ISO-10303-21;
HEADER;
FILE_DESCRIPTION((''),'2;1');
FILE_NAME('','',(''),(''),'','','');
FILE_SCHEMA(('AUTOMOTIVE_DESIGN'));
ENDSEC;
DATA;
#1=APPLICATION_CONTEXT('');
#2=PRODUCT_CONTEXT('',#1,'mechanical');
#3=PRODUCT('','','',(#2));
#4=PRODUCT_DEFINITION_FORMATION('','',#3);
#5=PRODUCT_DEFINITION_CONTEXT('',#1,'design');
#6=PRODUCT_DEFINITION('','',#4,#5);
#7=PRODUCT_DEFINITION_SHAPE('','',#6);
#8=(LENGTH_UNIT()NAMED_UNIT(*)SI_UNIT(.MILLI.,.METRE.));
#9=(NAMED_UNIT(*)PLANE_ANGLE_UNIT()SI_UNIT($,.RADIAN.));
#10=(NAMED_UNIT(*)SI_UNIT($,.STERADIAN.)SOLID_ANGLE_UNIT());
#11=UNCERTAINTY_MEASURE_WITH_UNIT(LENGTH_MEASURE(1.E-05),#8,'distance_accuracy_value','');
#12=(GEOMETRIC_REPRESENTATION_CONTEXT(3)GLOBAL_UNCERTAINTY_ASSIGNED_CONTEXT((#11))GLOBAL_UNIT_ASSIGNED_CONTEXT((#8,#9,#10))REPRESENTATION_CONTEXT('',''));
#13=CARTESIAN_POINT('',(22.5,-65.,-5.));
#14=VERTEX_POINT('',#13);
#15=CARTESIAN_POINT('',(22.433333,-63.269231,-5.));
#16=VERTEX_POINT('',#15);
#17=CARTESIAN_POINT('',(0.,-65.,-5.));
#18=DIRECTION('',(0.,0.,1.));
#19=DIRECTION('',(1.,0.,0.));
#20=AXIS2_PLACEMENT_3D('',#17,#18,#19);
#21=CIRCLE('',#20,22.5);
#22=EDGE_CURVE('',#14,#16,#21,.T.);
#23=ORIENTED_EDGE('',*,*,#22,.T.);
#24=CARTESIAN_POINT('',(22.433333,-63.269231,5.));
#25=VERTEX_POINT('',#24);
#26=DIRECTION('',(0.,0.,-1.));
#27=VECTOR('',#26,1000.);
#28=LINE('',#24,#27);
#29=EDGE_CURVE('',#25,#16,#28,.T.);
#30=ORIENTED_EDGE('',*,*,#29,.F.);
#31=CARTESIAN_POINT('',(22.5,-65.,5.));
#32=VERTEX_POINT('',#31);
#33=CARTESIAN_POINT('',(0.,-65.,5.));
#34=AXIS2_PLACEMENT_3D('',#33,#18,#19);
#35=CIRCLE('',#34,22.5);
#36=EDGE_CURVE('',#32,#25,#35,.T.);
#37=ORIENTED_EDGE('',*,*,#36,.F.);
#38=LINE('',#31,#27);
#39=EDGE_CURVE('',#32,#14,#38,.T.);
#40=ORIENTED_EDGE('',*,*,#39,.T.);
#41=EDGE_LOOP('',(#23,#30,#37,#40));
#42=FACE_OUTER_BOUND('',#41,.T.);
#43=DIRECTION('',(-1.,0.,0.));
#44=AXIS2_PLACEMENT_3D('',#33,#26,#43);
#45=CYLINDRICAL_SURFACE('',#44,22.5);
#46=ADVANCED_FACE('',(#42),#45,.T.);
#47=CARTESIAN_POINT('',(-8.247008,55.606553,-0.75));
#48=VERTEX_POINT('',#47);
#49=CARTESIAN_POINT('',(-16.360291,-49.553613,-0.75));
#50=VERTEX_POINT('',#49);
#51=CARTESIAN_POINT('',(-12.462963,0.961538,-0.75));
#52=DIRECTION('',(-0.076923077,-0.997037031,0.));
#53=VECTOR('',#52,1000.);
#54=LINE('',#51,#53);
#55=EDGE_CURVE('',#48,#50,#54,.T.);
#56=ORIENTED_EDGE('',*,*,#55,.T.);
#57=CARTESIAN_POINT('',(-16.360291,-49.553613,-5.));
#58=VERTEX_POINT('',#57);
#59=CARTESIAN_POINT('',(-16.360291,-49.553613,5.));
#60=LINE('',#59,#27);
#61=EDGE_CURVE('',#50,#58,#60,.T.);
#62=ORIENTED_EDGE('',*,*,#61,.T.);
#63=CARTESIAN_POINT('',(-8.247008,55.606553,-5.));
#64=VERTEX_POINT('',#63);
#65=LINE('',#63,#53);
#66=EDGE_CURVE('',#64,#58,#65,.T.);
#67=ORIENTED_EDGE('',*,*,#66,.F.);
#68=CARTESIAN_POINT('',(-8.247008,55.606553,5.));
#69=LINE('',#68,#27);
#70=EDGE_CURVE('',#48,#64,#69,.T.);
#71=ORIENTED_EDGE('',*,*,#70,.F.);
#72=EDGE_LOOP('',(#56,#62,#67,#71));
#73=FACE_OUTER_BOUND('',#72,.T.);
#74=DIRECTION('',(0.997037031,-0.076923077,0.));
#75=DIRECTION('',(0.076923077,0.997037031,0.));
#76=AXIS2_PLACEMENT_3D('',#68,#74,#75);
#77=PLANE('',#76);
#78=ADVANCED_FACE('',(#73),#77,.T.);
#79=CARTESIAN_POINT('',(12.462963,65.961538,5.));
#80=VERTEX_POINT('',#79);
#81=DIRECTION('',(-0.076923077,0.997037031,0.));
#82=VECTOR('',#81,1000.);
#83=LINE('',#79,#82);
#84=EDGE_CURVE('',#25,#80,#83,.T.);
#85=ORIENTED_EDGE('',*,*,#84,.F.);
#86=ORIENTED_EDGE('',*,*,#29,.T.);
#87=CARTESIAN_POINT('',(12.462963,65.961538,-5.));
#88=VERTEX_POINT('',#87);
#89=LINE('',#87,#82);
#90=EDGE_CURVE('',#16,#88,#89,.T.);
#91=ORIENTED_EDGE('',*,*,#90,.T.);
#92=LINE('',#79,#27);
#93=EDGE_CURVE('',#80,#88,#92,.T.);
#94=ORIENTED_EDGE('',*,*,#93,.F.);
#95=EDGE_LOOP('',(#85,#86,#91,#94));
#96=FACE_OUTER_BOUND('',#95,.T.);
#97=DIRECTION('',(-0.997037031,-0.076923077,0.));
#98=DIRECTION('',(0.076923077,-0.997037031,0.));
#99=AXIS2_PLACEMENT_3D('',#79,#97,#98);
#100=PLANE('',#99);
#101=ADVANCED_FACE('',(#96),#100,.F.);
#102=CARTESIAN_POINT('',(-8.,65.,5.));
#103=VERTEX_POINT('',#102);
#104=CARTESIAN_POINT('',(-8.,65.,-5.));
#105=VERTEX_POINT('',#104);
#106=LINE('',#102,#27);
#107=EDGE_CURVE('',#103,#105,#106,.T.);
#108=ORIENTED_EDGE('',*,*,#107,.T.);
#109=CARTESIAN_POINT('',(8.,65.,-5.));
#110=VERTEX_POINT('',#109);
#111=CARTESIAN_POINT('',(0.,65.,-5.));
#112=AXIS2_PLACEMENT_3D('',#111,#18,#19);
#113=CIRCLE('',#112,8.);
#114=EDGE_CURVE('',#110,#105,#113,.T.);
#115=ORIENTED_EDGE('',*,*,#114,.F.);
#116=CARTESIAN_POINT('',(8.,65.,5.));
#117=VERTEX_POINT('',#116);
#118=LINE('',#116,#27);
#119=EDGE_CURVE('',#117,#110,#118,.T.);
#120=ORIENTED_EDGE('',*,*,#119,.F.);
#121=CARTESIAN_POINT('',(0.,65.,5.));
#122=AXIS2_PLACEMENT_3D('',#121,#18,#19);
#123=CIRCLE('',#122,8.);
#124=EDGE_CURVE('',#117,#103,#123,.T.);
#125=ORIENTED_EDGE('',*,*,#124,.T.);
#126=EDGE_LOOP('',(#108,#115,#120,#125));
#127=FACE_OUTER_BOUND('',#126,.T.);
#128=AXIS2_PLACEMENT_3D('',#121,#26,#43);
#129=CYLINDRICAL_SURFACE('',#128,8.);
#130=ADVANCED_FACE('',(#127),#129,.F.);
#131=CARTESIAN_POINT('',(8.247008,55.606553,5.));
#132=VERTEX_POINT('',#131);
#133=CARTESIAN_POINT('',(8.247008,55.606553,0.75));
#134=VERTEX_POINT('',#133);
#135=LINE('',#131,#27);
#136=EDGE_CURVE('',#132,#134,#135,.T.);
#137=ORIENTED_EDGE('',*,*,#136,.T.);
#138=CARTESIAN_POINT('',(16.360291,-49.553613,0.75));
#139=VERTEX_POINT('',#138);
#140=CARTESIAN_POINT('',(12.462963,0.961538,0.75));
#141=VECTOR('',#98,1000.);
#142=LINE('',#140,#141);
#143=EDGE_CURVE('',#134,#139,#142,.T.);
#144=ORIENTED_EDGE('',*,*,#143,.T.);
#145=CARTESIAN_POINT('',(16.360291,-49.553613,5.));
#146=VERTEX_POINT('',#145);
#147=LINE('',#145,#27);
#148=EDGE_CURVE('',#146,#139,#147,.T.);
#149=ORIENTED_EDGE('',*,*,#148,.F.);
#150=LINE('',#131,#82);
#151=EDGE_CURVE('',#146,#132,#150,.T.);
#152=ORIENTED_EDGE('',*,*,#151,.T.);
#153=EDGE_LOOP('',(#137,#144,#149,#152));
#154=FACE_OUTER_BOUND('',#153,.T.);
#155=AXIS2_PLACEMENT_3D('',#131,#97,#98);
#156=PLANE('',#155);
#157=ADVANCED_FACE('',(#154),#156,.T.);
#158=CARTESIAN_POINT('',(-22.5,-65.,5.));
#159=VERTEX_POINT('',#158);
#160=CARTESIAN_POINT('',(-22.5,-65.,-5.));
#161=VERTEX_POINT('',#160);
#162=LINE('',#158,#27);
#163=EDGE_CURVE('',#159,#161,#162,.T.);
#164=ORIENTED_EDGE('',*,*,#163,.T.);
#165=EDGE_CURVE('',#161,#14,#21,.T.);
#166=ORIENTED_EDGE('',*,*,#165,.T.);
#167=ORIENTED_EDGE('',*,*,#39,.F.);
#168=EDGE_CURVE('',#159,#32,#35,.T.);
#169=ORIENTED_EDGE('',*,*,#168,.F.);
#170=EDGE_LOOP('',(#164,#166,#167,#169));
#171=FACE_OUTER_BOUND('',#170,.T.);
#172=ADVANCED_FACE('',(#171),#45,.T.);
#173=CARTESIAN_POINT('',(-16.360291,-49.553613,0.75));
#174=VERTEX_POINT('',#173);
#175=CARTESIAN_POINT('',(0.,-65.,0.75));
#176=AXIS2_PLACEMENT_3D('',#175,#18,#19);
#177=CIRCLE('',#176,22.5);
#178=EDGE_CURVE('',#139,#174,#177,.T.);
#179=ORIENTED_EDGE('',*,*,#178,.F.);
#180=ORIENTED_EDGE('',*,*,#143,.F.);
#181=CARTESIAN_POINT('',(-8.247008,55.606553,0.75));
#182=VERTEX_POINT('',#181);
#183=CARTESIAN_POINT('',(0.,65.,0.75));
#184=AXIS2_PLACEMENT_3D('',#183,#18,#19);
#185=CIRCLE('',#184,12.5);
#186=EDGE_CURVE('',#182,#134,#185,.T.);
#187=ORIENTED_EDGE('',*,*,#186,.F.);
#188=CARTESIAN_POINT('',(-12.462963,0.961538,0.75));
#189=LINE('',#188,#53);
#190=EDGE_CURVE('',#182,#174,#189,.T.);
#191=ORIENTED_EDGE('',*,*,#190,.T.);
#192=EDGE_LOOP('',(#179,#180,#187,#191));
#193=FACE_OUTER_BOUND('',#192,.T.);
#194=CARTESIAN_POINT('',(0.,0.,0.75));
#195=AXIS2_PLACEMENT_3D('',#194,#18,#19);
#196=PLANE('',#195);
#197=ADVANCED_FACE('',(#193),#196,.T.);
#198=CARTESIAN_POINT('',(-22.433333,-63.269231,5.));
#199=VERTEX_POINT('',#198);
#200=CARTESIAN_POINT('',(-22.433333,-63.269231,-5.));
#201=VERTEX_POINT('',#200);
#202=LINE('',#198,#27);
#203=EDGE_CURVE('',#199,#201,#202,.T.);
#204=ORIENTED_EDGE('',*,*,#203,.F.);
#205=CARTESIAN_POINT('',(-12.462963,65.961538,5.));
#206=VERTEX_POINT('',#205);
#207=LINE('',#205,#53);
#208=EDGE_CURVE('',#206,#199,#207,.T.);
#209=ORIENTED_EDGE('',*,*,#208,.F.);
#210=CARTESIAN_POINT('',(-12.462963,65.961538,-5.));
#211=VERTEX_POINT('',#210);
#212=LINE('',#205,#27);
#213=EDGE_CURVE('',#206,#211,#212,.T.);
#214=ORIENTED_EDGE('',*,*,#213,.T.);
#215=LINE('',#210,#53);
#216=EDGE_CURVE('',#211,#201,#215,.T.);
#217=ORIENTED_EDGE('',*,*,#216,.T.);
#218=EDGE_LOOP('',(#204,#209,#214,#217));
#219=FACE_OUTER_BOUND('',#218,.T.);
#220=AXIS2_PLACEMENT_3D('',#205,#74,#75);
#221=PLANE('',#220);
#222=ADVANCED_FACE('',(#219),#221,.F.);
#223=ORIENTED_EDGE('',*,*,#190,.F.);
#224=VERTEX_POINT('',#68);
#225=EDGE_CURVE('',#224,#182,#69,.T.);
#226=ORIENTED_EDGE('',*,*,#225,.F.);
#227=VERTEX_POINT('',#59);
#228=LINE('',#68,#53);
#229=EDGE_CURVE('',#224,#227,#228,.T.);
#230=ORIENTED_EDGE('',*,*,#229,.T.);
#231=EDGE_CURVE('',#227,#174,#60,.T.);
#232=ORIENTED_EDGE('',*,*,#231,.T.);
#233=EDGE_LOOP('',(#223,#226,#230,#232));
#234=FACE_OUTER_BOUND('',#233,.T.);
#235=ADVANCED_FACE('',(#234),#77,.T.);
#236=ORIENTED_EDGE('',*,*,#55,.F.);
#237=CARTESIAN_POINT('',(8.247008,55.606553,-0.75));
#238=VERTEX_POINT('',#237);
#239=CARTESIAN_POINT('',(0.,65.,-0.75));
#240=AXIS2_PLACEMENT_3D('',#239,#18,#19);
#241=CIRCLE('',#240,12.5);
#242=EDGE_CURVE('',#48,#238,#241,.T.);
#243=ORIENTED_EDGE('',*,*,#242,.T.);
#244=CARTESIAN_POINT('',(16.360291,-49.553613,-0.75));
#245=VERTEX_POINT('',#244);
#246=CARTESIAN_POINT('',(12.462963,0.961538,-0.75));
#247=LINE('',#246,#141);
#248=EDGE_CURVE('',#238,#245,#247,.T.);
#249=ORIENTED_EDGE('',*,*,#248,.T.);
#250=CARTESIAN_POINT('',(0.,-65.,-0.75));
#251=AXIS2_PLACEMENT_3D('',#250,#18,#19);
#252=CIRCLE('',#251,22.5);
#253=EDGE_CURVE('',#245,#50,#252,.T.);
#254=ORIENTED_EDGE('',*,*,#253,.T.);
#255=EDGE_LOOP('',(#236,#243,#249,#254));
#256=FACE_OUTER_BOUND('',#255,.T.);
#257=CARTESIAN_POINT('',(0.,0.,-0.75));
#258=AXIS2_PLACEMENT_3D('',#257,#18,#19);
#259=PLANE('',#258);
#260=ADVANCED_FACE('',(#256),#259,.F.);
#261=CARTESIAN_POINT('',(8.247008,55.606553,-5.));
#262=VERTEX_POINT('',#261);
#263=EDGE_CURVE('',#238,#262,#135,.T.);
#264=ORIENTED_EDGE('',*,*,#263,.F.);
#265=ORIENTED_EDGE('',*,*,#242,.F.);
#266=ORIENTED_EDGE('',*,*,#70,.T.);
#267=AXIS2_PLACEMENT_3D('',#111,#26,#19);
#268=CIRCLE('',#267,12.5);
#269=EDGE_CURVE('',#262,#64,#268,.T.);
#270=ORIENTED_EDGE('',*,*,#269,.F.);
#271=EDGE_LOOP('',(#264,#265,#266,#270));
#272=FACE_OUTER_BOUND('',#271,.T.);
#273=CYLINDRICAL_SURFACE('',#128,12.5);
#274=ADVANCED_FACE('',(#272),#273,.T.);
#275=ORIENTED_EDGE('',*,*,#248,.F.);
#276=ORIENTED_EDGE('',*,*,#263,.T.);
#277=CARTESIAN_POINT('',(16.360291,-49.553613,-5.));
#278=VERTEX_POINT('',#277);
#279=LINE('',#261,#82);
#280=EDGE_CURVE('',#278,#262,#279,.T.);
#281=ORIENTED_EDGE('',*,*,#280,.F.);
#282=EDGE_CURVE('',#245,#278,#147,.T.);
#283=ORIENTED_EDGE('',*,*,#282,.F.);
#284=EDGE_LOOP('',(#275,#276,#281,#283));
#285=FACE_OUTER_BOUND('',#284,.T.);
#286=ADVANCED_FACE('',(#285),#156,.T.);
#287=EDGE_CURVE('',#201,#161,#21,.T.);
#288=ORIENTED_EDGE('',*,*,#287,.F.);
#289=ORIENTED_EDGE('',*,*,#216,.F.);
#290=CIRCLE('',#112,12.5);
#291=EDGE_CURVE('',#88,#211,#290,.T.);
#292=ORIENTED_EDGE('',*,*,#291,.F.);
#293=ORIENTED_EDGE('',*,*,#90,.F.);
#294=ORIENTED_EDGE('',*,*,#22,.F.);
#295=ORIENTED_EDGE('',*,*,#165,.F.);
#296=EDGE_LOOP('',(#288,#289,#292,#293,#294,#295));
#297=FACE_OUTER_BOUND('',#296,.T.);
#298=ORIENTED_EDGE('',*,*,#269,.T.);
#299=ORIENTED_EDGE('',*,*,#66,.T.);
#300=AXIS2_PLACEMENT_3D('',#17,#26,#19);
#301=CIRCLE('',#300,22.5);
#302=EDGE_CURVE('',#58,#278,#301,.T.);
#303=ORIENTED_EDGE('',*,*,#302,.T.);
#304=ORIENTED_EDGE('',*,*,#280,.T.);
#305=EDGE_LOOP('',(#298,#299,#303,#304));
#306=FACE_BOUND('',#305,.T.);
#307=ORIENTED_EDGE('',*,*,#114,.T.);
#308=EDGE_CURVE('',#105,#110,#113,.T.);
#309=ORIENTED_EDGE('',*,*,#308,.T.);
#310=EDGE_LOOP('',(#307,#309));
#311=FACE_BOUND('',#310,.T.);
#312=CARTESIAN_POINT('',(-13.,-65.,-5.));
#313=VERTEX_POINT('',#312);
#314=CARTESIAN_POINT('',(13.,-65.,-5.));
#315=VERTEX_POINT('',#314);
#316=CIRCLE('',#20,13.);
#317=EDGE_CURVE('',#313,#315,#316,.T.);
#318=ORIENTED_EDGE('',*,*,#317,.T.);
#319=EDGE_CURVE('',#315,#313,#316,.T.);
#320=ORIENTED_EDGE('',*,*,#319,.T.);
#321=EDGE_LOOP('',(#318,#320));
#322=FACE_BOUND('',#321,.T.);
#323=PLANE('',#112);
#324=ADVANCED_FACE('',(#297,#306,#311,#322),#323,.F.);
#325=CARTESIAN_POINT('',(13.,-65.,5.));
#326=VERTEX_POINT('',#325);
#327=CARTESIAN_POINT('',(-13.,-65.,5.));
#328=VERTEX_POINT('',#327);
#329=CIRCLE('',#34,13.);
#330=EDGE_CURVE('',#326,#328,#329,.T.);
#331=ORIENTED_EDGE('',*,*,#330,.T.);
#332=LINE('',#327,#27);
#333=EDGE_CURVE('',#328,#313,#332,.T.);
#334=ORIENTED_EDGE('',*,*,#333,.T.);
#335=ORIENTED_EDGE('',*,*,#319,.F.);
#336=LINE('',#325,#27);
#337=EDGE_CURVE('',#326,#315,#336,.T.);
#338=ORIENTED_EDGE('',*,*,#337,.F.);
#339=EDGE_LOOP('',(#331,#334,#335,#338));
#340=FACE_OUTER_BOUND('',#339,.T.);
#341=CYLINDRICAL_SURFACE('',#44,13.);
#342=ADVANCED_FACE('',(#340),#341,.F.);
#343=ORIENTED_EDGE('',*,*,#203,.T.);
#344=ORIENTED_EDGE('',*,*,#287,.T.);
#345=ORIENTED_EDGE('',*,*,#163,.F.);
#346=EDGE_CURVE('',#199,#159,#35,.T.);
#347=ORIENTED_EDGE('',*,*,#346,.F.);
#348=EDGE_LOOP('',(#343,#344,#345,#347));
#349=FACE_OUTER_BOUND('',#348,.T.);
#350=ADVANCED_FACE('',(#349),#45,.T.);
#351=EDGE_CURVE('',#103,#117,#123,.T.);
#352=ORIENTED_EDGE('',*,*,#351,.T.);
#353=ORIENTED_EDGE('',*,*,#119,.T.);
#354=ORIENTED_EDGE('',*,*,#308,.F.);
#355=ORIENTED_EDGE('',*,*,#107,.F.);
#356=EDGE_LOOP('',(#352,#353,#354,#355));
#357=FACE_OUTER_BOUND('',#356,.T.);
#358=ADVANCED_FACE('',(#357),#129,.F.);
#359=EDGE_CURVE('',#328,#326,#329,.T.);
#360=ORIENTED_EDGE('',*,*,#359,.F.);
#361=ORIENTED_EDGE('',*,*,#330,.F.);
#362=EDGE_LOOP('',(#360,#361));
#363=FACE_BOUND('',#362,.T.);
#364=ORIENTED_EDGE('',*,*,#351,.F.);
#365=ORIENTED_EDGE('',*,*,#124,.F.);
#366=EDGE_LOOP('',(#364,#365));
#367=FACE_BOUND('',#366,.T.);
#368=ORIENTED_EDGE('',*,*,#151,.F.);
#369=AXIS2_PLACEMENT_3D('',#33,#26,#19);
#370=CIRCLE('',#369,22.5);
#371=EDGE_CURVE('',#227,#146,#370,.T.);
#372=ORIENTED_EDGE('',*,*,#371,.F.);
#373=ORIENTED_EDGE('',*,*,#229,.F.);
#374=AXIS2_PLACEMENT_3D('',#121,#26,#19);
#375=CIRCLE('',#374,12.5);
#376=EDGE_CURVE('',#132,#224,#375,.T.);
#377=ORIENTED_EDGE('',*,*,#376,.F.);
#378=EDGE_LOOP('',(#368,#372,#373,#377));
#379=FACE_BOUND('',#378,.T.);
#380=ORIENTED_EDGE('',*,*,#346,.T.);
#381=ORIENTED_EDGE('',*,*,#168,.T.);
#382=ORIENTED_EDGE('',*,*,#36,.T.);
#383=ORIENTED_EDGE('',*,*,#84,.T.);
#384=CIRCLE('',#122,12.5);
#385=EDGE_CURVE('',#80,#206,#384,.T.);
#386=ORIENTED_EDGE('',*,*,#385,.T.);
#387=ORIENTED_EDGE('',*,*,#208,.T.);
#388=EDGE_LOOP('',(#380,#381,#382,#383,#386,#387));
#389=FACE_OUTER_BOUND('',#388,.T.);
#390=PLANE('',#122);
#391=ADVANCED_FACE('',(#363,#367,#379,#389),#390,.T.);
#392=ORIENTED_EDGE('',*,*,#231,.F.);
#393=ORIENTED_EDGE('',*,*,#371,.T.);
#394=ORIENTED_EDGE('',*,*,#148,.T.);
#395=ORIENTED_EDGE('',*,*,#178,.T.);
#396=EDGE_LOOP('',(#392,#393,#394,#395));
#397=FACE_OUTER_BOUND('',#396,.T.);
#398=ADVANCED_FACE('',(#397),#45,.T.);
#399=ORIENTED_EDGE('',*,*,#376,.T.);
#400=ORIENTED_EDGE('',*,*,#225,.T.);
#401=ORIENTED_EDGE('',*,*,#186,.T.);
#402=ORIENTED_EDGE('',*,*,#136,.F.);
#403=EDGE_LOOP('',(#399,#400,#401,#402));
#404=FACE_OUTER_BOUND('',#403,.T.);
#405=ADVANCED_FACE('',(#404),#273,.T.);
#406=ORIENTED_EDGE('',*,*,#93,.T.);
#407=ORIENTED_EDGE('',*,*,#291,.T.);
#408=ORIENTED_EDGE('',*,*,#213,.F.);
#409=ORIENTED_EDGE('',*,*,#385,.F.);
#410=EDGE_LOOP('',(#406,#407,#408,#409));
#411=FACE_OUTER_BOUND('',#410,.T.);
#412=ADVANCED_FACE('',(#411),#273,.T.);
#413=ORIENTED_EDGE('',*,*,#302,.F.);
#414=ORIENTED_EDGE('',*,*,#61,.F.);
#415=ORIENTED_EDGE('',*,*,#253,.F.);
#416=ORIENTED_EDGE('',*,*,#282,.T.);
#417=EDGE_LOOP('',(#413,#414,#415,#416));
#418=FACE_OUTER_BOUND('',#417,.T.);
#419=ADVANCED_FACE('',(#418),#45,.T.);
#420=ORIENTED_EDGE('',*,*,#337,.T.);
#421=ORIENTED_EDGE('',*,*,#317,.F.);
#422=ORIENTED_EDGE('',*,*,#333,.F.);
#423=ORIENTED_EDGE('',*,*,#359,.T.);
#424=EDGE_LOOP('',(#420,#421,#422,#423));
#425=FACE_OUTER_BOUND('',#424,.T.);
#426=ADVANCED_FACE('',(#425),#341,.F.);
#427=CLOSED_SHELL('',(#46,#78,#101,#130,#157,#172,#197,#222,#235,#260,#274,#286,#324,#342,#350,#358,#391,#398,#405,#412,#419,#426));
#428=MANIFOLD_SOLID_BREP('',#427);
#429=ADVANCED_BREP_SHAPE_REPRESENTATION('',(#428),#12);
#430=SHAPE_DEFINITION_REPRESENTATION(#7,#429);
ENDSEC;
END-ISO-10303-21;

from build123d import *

# Parameters (mm, degrees)
ROD_PROFILE_SKETCH_R   = 8
ROD_PROFILE_SKETCH_R_2 = 13
ROD_BODY_10MM_DEPTH    = 5
WEB_RECESS_1_5MM_DEPTH = 0.75


with BuildPart() as part:
    # Rod Profile Sketch → Rod Body 10mm (new, symmetric)
    with BuildSketch(Plane.XY):
        with BuildLine():
            Line((-12.462962882, 65.961538462), (-22.433333187, -63.269230769))
            ThreePointArc((-22.433333187, -63.269230769), (0, -87.5), (22.433333187, -63.269230769))
            Line((22.433333187, -63.269230769), (12.462962882, 65.961538462))
            ThreePointArc((12.462962882, 65.961538462), (0, 77.5), (-12.462962882, 65.961538462))
        make_face()
        with Locations((0, 65)):
            Circle(ROD_PROFILE_SKETCH_R, mode=Mode.SUBTRACT)
        with Locations((0, -65)):
            Circle(ROD_PROFILE_SKETCH_R_2, mode=Mode.SUBTRACT)
        with BuildLine():
            Line((-8.247008498, 55.606552772), (-16.360291448, -49.553613246))
            ThreePointArc((-16.360291448, -49.553613246), (0, -42.5), (16.360291448, -49.553613246))
            Line((16.360291448, -49.553613246), (8.247008498, 55.606552772))
            ThreePointArc((8.247008498, 55.606552772), (0, 52.5), (-8.247008498, 55.606552772))
        make_face(mode=Mode.SUBTRACT)
    extrude(amount=ROD_BODY_10MM_DEPTH, both=True)

    # Sketch1_3 → Web Recess 1.5mm (add, symmetric)
    with BuildSketch(Plane.XY):
        with BuildLine():
            ThreePointArc((16.360291448, -49.553613246), (0, -42.5), (-16.360291448, -49.553613246))
            Line((-16.360291448, -49.553613246), (-8.247008498, 55.606552772))
            ThreePointArc((-8.247008498, 55.606552772), (0, 52.5), (8.247008498, 55.606552772))
            Line((8.247008498, 55.606552772), (16.360291448, -49.553613246))
        make_face()
    extrude(amount=WEB_RECESS_1_5MM_DEPTH, both=True)


solid = part.part
